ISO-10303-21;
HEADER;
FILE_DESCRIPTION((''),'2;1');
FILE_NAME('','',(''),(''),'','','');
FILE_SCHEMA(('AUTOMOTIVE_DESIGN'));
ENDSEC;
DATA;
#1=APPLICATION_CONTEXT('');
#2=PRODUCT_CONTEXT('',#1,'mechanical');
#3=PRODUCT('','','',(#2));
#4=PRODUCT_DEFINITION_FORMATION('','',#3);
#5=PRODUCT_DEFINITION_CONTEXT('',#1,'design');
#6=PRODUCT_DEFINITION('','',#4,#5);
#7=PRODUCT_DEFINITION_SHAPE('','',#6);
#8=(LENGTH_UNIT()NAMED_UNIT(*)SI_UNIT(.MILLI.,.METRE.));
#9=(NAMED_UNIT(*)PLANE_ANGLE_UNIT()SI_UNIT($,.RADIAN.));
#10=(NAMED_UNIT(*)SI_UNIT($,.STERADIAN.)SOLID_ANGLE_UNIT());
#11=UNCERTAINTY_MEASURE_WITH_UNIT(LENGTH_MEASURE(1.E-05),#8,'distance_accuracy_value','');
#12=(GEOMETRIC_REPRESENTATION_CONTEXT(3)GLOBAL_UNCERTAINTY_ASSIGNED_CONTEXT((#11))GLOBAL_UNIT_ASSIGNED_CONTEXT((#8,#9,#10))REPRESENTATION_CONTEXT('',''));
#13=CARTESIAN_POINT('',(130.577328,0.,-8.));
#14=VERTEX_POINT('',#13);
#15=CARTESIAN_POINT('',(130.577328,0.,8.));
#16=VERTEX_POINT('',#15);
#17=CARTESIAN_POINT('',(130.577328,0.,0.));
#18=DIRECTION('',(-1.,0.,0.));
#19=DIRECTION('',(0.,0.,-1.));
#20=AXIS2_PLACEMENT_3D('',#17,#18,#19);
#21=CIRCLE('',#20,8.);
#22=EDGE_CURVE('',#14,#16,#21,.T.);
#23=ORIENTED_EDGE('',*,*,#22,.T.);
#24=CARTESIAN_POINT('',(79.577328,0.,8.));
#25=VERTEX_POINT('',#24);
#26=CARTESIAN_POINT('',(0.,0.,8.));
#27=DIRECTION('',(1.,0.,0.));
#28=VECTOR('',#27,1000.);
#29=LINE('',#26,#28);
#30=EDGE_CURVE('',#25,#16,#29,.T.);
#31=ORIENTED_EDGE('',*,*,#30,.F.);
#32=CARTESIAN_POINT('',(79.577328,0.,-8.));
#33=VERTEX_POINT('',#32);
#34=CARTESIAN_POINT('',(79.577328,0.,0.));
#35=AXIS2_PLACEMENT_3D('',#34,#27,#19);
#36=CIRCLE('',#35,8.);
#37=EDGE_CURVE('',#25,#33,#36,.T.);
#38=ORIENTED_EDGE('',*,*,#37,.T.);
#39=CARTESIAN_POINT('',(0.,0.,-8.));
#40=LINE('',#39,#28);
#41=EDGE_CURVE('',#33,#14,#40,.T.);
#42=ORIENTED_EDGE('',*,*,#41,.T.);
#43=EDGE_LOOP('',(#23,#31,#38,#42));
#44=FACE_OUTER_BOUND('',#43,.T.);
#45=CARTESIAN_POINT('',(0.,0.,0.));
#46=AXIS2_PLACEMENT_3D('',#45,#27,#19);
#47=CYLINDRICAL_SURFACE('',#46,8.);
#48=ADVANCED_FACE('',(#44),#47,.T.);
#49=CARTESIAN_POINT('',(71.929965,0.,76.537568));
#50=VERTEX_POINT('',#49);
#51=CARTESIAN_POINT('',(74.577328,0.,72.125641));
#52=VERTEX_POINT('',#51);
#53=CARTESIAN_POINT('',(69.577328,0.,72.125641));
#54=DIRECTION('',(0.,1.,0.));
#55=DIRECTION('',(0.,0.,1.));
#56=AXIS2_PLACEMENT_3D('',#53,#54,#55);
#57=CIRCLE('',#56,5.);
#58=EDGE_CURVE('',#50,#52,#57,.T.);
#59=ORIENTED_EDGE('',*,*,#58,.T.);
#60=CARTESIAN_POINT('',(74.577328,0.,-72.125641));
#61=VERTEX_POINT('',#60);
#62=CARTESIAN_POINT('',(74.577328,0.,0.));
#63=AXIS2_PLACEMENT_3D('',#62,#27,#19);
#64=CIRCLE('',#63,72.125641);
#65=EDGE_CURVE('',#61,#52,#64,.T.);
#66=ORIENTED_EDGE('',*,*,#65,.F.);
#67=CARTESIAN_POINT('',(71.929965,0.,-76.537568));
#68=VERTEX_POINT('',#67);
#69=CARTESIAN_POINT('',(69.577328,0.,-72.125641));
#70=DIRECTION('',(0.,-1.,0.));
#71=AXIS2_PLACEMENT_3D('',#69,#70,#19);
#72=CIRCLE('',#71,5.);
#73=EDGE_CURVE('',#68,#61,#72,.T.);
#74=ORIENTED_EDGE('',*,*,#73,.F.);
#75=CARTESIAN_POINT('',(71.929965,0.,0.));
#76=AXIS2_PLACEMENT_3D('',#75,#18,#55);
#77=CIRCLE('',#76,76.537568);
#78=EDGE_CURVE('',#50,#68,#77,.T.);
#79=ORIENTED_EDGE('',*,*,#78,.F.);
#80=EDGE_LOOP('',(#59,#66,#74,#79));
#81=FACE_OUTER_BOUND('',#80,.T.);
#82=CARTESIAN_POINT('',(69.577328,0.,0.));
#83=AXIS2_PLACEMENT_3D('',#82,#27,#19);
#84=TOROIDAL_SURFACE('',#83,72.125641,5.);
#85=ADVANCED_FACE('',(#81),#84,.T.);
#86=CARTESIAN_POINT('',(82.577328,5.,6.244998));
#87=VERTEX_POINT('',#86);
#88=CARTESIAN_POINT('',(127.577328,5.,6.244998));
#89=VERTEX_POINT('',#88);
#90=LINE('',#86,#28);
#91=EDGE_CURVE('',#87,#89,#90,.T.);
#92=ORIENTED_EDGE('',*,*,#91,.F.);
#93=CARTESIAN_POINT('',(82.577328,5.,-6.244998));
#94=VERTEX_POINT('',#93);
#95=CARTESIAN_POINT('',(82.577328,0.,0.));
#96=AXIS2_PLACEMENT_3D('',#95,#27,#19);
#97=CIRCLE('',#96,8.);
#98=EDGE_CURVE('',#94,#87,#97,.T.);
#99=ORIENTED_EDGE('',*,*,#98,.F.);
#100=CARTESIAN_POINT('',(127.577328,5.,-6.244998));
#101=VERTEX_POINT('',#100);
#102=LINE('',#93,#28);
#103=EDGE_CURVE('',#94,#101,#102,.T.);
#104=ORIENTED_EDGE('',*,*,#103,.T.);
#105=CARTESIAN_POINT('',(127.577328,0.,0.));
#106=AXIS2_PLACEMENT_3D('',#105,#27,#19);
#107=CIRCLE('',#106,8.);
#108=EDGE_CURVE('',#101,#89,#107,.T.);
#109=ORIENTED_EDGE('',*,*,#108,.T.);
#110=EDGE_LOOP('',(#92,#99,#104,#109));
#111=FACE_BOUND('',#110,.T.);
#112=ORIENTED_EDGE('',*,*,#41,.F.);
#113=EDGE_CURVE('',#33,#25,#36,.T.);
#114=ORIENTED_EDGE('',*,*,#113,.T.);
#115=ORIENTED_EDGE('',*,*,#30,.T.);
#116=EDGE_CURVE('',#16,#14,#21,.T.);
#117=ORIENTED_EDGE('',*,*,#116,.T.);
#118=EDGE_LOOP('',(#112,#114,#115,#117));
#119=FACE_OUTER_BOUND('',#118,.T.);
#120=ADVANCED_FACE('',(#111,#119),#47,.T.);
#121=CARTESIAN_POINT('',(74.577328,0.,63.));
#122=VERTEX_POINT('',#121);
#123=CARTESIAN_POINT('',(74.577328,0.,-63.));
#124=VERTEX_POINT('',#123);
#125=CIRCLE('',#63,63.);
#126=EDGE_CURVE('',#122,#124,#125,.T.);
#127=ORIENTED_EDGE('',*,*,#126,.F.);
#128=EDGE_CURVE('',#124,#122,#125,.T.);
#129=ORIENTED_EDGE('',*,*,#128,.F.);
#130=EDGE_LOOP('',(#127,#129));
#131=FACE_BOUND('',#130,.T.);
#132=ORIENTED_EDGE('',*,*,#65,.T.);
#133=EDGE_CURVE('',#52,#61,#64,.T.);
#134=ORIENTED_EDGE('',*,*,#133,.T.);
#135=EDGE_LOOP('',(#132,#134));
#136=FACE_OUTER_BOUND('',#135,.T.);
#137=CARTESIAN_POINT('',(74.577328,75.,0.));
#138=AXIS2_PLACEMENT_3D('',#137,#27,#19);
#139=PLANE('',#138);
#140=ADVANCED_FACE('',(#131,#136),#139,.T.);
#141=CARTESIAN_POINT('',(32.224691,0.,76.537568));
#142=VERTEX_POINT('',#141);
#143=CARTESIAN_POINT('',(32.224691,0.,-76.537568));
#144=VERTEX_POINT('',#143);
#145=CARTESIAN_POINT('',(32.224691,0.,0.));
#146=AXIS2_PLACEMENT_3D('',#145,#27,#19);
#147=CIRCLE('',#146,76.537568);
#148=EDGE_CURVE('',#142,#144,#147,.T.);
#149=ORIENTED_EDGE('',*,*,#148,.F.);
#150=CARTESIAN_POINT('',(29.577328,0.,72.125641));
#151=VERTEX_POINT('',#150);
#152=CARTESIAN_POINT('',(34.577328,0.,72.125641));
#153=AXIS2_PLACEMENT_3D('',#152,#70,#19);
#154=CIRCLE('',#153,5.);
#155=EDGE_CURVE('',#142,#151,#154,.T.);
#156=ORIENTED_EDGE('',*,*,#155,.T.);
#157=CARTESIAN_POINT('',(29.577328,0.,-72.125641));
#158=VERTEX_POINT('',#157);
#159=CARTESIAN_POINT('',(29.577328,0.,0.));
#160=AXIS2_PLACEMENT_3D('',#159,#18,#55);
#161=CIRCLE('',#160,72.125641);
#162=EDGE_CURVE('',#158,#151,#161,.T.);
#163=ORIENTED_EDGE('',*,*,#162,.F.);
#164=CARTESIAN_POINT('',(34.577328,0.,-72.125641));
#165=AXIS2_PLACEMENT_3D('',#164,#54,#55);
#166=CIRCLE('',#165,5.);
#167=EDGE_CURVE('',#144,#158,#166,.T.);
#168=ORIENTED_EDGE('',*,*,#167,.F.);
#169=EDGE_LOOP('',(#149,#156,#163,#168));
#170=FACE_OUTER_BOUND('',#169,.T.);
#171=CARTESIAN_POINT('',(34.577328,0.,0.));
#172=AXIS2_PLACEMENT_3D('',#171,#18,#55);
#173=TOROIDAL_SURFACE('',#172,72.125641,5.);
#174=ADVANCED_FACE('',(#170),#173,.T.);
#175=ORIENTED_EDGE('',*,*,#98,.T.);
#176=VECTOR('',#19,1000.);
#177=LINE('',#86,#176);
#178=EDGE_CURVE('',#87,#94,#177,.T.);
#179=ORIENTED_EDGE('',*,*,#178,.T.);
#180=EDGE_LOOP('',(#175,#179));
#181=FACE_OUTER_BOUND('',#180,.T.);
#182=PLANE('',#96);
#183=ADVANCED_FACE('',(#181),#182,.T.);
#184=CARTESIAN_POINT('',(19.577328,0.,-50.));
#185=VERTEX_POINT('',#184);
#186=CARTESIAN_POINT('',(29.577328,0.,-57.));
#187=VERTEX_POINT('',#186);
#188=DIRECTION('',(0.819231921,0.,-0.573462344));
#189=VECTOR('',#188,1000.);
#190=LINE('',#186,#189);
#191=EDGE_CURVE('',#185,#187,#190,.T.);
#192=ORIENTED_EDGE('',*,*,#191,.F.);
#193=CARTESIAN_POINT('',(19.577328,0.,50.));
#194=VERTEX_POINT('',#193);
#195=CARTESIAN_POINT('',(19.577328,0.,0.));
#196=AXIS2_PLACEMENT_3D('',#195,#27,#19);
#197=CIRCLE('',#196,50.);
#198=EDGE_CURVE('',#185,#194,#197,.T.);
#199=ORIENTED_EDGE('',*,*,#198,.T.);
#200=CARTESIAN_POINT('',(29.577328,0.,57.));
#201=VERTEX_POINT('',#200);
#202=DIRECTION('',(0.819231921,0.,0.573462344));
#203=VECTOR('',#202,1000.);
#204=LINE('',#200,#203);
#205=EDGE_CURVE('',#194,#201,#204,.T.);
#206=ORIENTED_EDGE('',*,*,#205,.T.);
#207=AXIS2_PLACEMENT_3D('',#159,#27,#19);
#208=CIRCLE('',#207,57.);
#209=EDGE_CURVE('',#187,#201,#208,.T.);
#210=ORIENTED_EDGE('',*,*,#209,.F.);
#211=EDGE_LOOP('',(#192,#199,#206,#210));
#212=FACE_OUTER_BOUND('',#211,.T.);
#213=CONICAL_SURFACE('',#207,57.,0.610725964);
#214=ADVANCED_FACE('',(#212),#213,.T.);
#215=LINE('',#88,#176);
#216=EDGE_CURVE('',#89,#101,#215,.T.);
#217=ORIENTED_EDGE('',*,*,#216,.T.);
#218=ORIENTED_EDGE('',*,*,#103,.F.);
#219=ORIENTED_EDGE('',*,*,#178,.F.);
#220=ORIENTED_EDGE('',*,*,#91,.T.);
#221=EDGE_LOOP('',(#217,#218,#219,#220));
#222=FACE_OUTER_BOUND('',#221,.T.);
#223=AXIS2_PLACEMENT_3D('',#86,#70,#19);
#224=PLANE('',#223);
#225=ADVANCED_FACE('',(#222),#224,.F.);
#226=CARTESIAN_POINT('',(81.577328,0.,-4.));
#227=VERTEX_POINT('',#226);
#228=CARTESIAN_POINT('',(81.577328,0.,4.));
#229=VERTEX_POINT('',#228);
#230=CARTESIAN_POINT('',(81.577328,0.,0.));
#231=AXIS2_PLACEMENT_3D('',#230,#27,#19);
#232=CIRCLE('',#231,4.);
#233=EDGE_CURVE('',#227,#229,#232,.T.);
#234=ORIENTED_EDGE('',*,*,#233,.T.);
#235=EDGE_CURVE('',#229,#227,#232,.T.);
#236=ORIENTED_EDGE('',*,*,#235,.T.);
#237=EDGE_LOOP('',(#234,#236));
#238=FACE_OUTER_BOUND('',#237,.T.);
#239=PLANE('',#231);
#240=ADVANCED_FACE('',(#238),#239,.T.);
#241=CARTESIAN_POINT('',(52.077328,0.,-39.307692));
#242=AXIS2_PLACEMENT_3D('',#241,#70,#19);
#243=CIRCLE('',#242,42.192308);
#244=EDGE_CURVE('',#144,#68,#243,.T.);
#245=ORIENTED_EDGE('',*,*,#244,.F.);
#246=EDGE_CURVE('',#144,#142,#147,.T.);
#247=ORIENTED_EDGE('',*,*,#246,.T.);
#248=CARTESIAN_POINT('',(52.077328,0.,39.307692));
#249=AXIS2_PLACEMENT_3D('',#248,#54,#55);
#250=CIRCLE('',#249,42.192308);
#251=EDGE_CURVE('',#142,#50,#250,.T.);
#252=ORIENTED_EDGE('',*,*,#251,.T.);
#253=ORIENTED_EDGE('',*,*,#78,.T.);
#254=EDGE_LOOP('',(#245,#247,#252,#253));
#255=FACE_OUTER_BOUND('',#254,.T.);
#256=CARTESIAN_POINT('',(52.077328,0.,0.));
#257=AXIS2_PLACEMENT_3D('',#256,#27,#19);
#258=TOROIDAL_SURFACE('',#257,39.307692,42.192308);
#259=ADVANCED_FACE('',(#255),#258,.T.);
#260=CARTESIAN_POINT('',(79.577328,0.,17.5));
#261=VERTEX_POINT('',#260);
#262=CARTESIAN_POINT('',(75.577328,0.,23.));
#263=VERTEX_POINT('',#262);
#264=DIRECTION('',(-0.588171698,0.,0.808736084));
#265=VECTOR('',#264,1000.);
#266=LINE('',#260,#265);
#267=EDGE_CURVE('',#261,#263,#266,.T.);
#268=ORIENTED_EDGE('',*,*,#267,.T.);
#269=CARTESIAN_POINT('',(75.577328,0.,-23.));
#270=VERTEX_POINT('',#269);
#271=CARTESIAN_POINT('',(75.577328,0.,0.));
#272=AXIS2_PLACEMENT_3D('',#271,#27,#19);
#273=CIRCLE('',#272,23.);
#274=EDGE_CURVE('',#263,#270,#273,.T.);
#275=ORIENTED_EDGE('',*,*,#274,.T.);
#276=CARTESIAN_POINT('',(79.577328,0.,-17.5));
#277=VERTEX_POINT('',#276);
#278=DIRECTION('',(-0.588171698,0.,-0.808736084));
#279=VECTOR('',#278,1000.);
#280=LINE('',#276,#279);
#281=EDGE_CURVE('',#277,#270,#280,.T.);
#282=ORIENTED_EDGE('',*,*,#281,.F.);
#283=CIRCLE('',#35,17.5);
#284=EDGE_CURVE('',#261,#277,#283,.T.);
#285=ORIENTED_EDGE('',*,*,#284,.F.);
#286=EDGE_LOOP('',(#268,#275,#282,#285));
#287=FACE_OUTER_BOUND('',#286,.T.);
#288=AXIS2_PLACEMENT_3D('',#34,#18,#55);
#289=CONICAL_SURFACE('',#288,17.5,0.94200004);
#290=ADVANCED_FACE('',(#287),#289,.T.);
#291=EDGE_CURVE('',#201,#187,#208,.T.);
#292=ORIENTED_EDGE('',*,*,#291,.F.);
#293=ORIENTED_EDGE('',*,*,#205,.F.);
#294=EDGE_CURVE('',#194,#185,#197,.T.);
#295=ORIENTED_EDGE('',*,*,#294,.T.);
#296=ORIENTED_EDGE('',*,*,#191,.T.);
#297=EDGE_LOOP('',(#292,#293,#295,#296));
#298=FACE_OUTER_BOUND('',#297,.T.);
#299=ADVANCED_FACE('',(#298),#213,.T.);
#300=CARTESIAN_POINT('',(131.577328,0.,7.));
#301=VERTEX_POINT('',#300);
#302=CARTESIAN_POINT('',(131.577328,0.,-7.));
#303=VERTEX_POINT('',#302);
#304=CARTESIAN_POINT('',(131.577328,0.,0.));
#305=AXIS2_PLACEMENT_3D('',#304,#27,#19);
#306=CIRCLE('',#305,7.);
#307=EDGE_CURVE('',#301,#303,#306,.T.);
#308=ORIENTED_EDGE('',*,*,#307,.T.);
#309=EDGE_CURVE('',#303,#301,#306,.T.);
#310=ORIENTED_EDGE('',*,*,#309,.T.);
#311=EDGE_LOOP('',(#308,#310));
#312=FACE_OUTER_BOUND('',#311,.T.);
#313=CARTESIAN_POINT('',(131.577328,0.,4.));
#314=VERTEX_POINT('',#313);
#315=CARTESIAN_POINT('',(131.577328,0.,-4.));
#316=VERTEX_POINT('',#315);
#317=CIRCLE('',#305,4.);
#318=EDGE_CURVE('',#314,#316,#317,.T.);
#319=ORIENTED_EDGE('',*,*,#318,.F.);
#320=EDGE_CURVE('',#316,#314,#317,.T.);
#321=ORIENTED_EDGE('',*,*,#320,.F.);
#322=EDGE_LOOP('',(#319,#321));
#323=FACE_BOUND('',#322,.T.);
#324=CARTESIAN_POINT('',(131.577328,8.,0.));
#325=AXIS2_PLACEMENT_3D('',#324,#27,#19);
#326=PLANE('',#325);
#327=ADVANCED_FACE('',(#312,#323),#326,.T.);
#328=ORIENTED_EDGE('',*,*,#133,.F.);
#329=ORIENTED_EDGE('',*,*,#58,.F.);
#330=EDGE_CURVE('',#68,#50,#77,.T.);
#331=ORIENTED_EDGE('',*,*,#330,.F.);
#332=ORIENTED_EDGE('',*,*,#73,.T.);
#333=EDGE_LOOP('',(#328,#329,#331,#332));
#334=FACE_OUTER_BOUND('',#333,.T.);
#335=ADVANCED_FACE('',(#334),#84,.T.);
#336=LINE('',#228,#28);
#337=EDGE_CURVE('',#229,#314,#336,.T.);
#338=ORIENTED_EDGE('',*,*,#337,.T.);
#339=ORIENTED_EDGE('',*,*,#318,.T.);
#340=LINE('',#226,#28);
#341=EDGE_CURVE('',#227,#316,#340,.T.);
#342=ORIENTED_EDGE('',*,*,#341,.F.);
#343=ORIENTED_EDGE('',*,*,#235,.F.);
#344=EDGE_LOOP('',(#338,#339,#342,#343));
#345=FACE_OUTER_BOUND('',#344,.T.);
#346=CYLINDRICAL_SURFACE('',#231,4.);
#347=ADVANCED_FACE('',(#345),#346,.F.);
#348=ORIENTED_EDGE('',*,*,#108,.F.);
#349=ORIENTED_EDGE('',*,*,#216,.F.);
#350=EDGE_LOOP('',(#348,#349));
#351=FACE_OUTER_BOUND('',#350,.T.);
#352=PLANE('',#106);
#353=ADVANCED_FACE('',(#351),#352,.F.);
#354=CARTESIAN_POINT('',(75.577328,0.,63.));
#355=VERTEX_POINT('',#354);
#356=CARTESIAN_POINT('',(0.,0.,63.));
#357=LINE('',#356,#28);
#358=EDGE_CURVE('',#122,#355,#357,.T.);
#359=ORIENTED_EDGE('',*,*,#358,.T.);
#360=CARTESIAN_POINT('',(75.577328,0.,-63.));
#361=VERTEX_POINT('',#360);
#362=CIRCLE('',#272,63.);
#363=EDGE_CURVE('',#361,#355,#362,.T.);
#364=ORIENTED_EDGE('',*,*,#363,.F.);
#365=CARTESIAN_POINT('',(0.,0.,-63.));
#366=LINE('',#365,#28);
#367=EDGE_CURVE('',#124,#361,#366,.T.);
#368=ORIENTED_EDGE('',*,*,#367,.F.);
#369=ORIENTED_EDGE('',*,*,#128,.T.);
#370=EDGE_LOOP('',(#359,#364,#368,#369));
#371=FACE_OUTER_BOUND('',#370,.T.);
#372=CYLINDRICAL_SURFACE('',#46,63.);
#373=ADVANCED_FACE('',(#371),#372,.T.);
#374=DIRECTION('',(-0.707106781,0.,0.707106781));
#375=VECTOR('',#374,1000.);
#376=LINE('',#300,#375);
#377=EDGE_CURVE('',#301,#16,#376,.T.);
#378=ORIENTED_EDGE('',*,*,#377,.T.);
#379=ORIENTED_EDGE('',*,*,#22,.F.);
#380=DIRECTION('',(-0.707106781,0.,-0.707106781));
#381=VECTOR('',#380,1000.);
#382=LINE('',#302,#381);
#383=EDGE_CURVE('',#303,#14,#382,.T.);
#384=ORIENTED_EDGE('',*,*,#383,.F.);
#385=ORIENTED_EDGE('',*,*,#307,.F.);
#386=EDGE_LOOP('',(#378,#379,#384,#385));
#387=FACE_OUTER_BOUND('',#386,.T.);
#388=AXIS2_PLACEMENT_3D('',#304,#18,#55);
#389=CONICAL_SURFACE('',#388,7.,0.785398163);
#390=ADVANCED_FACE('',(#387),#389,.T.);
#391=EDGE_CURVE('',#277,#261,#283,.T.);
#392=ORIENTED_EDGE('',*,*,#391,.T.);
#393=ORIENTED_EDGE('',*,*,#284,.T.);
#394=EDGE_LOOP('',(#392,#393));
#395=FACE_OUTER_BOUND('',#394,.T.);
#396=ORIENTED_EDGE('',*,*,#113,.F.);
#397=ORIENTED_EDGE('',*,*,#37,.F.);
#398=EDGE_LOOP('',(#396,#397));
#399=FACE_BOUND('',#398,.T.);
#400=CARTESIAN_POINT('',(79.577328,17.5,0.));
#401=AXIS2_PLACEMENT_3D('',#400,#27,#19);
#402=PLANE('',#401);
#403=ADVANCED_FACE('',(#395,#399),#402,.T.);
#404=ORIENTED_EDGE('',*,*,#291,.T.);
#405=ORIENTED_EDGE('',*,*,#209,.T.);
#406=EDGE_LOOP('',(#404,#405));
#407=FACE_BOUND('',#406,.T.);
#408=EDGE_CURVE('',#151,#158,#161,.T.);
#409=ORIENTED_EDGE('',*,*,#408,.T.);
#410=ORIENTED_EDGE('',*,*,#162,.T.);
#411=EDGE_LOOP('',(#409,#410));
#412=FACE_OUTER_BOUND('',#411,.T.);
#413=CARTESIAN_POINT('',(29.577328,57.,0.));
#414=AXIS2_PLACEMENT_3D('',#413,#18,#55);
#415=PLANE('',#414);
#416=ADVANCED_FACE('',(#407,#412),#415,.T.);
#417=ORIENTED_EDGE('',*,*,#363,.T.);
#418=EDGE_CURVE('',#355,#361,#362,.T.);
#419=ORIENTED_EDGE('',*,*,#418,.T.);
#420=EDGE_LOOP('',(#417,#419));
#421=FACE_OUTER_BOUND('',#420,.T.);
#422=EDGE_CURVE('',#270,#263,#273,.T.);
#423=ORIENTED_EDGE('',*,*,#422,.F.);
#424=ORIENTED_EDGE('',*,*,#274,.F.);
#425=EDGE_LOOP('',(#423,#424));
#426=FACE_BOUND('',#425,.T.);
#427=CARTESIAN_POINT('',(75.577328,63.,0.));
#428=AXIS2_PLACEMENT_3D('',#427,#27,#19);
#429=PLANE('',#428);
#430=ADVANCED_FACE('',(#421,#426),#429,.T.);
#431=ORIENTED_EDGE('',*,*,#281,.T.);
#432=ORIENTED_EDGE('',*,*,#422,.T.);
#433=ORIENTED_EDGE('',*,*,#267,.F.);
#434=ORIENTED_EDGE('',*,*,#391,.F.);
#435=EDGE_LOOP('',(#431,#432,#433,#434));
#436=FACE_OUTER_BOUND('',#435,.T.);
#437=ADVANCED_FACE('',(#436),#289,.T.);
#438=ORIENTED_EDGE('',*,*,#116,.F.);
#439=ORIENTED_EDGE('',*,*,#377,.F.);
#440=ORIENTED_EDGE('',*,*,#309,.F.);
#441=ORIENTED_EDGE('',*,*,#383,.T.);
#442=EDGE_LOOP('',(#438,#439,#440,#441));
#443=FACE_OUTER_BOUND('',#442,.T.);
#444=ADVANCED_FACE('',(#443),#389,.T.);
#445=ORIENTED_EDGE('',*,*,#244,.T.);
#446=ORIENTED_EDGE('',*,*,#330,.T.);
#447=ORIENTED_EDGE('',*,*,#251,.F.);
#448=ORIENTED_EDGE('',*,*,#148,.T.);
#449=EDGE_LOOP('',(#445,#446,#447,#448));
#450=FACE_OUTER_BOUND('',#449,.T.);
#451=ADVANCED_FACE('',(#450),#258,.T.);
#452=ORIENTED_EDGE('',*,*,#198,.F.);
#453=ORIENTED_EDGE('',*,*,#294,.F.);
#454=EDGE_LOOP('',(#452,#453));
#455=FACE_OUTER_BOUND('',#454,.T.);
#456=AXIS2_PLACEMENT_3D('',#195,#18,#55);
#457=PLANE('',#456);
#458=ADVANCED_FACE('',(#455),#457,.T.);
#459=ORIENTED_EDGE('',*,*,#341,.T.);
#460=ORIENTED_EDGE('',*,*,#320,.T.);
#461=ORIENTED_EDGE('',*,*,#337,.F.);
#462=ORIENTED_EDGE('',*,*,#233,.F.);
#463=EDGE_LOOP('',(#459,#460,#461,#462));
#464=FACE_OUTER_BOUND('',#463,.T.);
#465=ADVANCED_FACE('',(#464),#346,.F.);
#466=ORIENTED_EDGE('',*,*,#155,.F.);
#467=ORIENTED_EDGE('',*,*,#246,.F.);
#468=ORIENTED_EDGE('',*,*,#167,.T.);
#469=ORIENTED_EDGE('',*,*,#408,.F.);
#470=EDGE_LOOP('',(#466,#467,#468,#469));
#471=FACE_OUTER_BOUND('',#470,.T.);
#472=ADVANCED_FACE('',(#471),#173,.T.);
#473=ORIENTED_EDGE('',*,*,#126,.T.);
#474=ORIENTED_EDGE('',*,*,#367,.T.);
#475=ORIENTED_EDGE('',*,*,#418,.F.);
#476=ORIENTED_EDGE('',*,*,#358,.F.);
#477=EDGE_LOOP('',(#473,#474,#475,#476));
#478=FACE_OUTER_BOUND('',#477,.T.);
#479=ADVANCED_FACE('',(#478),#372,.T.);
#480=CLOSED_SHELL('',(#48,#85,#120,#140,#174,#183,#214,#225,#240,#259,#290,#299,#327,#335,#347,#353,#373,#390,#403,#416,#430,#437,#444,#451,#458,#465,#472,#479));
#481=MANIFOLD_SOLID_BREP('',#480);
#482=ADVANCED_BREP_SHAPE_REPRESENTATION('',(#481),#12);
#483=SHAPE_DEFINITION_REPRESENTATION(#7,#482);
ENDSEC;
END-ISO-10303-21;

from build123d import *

# Parameters (mm, degrees)
FILLET1_R          = 5
CUT_EXTRUDE2_START = -4
CUT_EXTRUDE2_DEPTH = 45
CHAMFER1_SIZE      = 1
SKETCH4_R          = 4
CUT_EXTRUDE3_DEPTH = 50


with BuildPart() as part:
    # Sketch1 → Revolve1 (revolve)
    with BuildSketch(Plane.XY, mode=Mode.PRIVATE) as revolve1_sk:
        with BuildLine():
            Line((19.577327609, 0), (19.577327609, 50))
            Line((19.577327609, 50), (29.577327609, 57))
            Line((29.577327609, 57), (29.577327609, 75))
            ThreePointArc((29.577327609, 75), (52.077327609, 81.5), (74.577327609, 75))
            Line((74.577327609, 75), (74.577327609, 63))
            Line((74.577327609, 63), (75.577327609, 63))
            Line((75.577327609, 63), (75.577327609, 23))
            Line((75.577327609, 23), (79.577327609, 17.5))
            Line((79.577327609, 17.5), (79.577327609, 8))
            Line((79.577327609, 8), (131.577327609, 8))
            Line((131.577327609, 8), (131.577327609, 0))
            Line((131.577327609, 0), (19.577327609, 0))
        make_face()
    revolve(revolve1_sk.sketch.rotate(Axis((0, 0, 0), (-1, 0, 0)), 90), axis=Axis((0, 0, 0), (-1, 0, 0)))

    # Fillet1
    fillet1_edges = [part.edges().sort_by_distance(p)[0] for p in [
        (74.577327609, 0, 75),
        (29.577327609, 0, 75),
    ]]
    fillet(fillet1_edges, radius=FILLET1_R)

    # Sketch3 → Cut-Extrude2 (cut)
    with BuildSketch(Plane(origin=(131.577327609, 0, 0), x_dir=(0, 0, -1), z_dir=(1, 0, 0)).offset(CUT_EXTRUDE2_START)):
        with BuildLine():
            Line((-6.244997998, 5), (6.244997998, 5))
            ThreePointArc((6.244997998, 5), (0, 8), (-6.244997998, 5))
        make_face()
    extrude(amount=-CUT_EXTRUDE2_DEPTH, mode=Mode.SUBTRACT)

    # Chamfer1
    chamfer1_edges = [part.edges().sort_by_distance(p)[0] for p in [
        (131.577327609, 0, 8),
    ]]
    chamfer(chamfer1_edges, length=CHAMFER1_SIZE)

    # Sketch4 → Cut-Extrude3 (cut)
    with BuildSketch(Plane(origin=(131.577327609, 0, 0), x_dir=(0, 0, -1), z_dir=(1, 0, 0))):
        Circle(SKETCH4_R)
    extrude(amount=-CUT_EXTRUDE3_DEPTH, mode=Mode.SUBTRACT)


solid = part.part
